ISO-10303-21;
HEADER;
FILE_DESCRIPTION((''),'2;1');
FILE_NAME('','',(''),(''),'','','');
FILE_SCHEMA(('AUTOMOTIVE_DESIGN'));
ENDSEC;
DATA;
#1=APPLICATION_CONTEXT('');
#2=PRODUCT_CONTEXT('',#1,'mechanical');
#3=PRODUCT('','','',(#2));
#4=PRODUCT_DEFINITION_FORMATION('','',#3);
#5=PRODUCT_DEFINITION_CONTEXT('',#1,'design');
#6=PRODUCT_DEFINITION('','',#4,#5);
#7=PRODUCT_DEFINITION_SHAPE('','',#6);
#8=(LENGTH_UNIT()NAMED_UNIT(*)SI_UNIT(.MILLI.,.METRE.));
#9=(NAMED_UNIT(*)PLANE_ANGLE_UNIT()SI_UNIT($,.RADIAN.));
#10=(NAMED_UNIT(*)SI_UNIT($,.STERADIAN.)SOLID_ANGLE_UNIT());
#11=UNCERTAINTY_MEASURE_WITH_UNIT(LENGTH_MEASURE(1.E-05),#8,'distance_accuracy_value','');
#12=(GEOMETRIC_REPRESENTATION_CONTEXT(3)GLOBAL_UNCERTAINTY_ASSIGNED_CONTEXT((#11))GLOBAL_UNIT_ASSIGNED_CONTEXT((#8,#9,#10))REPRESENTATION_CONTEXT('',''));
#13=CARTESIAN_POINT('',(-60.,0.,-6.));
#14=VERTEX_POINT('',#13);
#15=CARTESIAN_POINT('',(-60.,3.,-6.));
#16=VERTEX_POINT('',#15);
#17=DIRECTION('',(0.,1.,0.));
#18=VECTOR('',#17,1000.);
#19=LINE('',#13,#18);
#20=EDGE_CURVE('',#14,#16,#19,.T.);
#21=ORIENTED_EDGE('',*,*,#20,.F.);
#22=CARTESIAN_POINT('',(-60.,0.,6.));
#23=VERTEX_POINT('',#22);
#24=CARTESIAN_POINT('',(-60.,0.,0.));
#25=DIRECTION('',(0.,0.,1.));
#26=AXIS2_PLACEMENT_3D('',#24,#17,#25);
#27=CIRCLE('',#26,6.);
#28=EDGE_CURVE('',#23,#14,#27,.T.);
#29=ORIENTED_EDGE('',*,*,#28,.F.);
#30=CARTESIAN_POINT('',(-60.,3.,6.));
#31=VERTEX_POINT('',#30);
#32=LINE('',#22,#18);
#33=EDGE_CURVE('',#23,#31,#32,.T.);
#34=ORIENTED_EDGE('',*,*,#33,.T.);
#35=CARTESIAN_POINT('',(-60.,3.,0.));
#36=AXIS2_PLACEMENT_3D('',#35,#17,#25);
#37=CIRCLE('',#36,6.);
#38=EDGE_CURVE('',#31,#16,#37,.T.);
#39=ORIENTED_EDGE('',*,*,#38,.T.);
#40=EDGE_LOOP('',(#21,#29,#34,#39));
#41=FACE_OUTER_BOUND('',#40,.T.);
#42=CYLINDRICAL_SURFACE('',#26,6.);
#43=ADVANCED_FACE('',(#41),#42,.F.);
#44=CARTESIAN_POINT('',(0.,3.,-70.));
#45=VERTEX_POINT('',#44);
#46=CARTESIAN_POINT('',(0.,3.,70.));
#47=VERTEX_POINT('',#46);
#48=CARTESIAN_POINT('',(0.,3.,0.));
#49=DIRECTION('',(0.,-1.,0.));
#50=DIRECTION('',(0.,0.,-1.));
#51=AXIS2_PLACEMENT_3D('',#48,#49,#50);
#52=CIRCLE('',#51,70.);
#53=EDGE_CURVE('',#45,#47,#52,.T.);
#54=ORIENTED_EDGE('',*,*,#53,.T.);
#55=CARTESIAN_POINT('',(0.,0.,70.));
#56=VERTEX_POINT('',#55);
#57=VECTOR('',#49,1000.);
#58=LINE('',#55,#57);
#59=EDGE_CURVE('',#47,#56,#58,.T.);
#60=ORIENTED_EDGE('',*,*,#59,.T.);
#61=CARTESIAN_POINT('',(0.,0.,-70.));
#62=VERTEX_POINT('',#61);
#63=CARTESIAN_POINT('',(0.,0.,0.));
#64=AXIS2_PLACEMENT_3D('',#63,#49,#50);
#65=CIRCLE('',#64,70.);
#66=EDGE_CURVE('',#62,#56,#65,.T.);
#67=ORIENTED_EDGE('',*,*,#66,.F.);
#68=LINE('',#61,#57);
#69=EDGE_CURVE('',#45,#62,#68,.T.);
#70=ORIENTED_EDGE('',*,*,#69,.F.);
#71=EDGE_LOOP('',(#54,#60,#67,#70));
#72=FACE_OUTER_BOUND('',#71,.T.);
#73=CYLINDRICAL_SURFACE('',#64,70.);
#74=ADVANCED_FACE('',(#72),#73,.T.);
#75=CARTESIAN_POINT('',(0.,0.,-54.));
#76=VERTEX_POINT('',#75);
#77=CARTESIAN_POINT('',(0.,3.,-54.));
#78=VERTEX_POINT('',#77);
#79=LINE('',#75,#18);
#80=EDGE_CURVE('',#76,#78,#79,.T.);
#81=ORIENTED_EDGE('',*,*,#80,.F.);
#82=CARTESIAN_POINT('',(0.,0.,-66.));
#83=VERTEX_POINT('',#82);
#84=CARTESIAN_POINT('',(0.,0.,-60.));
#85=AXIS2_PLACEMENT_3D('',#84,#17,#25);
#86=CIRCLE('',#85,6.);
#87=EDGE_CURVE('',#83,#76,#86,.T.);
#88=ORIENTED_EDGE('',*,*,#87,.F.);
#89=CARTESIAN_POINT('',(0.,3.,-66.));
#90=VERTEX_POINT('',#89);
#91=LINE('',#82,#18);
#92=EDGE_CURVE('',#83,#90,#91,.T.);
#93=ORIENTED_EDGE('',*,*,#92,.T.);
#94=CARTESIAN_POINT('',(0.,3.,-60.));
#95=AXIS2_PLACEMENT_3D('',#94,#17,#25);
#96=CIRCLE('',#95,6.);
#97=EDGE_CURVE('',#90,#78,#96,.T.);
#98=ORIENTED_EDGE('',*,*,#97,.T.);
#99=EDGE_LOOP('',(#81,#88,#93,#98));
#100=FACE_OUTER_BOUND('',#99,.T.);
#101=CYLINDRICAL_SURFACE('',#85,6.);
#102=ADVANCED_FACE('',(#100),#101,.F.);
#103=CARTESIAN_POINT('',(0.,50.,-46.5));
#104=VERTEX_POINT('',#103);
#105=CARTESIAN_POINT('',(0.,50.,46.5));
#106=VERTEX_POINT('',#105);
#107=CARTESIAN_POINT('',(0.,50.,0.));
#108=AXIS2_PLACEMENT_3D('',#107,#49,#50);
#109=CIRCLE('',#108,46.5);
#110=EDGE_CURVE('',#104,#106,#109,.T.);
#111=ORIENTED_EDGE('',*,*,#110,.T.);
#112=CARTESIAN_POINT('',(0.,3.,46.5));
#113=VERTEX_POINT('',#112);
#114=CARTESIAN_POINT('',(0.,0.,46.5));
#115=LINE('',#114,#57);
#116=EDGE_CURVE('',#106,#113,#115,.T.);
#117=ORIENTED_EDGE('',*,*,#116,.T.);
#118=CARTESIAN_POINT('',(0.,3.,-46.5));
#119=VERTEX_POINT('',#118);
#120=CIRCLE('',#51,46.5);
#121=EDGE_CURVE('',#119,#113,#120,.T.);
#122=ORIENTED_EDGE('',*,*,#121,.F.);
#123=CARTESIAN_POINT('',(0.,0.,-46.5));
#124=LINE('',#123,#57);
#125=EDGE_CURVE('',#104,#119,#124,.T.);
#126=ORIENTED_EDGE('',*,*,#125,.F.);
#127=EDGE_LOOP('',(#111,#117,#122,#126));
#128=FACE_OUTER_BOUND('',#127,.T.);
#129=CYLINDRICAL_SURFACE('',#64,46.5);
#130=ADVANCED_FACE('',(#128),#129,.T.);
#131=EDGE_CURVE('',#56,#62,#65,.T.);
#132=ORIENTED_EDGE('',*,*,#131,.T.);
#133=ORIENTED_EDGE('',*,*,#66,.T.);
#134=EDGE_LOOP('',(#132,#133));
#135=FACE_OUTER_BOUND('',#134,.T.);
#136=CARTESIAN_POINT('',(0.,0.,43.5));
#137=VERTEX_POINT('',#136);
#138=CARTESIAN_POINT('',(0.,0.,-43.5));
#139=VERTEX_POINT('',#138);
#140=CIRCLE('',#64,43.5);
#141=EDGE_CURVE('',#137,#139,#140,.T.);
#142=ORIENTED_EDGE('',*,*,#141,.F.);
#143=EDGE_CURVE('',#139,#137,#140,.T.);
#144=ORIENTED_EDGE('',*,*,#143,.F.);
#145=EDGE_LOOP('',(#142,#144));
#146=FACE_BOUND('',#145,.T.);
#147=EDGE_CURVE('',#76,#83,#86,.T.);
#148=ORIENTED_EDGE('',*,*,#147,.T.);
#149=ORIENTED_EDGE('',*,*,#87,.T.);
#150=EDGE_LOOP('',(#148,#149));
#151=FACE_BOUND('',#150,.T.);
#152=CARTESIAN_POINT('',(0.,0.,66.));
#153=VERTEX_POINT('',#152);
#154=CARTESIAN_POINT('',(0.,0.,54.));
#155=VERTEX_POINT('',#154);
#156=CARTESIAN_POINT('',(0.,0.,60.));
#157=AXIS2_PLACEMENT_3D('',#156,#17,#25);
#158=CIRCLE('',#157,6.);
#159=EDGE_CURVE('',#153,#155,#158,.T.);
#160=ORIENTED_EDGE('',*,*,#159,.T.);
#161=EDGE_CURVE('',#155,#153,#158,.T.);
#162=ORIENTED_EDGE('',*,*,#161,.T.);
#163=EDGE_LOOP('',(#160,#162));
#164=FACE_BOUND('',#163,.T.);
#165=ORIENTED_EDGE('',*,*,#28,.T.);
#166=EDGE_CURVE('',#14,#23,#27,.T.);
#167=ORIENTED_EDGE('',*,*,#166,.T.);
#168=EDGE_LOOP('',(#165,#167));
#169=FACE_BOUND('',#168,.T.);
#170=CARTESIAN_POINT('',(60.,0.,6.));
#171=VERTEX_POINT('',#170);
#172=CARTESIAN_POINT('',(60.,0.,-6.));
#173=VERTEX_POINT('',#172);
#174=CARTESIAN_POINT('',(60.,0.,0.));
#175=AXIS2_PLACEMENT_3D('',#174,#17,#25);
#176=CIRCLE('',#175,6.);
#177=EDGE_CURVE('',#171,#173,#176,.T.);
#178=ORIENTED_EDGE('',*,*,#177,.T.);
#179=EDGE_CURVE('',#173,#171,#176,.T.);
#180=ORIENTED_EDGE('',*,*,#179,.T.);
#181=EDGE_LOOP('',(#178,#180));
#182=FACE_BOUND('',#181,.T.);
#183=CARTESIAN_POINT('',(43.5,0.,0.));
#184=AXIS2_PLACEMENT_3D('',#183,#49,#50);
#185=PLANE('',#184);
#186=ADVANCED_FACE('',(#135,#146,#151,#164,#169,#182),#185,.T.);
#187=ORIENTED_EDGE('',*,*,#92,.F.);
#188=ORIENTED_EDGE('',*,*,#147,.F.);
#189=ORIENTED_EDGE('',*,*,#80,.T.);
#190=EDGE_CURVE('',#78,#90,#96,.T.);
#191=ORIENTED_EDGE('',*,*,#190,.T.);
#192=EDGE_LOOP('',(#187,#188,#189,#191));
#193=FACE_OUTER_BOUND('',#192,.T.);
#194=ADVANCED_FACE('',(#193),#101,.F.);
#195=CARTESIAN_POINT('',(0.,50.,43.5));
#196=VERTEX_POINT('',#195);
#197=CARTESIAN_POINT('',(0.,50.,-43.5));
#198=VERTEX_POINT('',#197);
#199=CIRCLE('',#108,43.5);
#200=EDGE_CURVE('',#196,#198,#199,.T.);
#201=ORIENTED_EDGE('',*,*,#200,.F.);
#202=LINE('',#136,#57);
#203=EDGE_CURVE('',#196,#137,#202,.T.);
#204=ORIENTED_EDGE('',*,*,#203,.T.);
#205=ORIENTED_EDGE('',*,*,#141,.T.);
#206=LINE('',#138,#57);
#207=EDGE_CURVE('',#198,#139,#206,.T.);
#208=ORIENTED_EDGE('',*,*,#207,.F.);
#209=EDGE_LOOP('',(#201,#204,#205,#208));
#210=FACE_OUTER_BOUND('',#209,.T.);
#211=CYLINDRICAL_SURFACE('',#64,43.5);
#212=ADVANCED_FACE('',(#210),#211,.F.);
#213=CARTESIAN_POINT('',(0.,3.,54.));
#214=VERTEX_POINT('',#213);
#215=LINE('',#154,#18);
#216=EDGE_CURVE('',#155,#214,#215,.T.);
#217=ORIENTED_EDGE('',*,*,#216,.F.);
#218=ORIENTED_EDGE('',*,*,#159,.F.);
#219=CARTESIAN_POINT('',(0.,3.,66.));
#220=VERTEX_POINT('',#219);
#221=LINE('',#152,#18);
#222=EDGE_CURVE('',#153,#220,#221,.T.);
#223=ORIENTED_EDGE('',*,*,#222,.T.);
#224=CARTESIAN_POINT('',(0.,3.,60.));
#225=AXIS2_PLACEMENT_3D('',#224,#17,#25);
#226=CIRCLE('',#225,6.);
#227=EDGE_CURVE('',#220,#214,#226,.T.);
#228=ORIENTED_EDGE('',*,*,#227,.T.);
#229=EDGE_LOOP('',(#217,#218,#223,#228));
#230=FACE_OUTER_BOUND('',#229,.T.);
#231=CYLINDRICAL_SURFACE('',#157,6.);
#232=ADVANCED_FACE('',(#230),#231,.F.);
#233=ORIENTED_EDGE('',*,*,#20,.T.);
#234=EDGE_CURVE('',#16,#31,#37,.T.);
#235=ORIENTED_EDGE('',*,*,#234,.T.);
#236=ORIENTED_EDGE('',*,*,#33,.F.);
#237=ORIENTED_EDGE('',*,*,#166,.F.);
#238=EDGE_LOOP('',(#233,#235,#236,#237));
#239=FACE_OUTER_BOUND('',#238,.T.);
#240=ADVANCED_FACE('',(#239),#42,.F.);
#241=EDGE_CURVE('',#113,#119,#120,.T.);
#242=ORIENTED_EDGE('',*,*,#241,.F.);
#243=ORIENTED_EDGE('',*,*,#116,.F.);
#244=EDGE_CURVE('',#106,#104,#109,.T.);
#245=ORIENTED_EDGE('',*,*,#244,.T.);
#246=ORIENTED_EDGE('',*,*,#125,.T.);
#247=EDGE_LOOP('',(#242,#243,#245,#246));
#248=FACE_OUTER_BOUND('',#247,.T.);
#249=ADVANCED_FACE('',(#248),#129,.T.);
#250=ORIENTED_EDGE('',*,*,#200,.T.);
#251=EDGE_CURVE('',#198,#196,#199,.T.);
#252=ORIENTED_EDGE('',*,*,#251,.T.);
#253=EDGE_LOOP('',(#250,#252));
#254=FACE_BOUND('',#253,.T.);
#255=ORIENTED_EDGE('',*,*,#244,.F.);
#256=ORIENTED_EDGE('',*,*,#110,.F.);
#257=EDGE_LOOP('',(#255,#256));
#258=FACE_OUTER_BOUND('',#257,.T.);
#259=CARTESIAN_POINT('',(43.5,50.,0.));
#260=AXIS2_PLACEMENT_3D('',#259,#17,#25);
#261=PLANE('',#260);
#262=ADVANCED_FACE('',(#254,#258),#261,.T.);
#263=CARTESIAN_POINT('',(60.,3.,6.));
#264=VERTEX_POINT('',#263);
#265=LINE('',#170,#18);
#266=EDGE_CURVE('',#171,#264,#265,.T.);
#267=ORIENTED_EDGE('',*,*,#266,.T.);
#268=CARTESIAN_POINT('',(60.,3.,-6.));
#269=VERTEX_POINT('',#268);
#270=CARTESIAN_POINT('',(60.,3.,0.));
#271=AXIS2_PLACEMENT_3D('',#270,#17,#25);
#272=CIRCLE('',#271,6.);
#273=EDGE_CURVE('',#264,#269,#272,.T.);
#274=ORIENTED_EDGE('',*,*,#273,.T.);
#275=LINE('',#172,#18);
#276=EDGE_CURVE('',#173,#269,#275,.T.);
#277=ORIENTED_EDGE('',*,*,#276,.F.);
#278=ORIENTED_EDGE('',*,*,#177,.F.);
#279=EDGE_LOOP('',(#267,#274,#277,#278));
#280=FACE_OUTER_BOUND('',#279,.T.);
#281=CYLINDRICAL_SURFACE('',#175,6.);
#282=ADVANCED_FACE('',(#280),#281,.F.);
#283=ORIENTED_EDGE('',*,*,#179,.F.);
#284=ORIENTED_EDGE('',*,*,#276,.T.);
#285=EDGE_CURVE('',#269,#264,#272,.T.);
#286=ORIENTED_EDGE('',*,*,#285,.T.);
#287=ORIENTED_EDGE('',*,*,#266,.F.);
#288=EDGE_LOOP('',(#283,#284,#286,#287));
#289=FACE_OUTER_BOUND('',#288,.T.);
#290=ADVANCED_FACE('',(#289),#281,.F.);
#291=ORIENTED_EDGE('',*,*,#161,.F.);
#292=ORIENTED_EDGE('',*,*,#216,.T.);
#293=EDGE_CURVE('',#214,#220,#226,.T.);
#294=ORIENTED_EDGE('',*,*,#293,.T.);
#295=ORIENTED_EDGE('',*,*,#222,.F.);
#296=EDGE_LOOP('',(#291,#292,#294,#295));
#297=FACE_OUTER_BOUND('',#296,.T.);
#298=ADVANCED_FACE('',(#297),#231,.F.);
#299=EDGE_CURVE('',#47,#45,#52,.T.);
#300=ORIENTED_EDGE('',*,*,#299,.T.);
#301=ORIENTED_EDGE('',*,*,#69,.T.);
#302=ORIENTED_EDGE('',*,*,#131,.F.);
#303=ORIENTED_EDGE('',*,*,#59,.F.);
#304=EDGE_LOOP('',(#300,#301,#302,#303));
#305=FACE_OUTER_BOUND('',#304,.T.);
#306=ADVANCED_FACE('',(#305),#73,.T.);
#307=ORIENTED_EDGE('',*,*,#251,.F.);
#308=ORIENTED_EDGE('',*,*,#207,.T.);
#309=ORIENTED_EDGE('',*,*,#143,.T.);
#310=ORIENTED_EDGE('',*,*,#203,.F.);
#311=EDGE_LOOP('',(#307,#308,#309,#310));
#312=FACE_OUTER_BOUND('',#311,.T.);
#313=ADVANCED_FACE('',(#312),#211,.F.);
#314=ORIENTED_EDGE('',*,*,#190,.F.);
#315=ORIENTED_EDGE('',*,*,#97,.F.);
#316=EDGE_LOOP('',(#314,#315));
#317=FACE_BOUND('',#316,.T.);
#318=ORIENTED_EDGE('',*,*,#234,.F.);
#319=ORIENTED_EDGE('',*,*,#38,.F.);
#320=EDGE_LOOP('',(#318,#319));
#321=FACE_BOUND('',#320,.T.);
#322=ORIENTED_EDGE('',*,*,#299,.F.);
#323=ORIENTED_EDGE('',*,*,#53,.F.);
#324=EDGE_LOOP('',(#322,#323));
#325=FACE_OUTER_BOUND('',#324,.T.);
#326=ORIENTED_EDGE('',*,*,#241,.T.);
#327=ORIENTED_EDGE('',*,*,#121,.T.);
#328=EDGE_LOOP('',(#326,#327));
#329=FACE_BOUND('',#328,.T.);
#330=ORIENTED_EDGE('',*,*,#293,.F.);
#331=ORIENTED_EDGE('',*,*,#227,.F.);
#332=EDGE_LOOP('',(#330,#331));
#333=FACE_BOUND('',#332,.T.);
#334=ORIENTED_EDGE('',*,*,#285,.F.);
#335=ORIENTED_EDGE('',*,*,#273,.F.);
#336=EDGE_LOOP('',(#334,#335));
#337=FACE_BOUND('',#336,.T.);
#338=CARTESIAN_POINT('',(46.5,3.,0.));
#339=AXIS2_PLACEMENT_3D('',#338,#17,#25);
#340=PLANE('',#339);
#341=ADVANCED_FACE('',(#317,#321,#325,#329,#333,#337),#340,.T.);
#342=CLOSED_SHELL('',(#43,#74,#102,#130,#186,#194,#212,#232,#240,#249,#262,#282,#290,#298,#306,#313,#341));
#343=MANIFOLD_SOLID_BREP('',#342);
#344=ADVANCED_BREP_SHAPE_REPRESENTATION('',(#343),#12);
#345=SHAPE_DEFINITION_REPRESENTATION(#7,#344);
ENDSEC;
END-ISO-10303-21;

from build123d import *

# Parameters (mm, degrees)
SKETCH_2_R          = 6
CUT_EXTRUDE_1_DEPTH = 110.585582993


with BuildPart() as part:
    # 草图1 → 旋转1 (revolve)
    with BuildSketch(Plane.XY, mode=Mode.PRIVATE) as revolve_1_sk:
        Polygon((43.5, 50), (43.5, 0), (70, 0), (70, 3), (46.5, 3), (46.5, 50), align=None)
    revolve(revolve_1_sk.sketch.rotate(Axis((0, 0, 0), (0, 1, 0)), 90), axis=Axis((0, 0, 0), (0, 1, 0)))

    # 草图2 → 切除-拉伸1 (cut, through all)
    with BuildSketch(Plane(origin=(0, 3, 0), x_dir=(1, 0, 0), z_dir=(0, 1, 0))):
        with Locations(Location((0, 60, 0), (0, 0, 270))):
            Circle(SKETCH_2_R)
        with Locations(Location((60, 0, 0), (0, 0, 270))):
            Circle(SKETCH_2_R)
        with Locations(Location((0, -60, 0), (0, 0, 270))):
            Circle(SKETCH_2_R)
        with Locations(Location((-60, 0, 0), (0, 0, 270))):
            Circle(SKETCH_2_R)
    extrude(amount=-CUT_EXTRUDE_1_DEPTH, mode=Mode.SUBTRACT)


solid = part.part
